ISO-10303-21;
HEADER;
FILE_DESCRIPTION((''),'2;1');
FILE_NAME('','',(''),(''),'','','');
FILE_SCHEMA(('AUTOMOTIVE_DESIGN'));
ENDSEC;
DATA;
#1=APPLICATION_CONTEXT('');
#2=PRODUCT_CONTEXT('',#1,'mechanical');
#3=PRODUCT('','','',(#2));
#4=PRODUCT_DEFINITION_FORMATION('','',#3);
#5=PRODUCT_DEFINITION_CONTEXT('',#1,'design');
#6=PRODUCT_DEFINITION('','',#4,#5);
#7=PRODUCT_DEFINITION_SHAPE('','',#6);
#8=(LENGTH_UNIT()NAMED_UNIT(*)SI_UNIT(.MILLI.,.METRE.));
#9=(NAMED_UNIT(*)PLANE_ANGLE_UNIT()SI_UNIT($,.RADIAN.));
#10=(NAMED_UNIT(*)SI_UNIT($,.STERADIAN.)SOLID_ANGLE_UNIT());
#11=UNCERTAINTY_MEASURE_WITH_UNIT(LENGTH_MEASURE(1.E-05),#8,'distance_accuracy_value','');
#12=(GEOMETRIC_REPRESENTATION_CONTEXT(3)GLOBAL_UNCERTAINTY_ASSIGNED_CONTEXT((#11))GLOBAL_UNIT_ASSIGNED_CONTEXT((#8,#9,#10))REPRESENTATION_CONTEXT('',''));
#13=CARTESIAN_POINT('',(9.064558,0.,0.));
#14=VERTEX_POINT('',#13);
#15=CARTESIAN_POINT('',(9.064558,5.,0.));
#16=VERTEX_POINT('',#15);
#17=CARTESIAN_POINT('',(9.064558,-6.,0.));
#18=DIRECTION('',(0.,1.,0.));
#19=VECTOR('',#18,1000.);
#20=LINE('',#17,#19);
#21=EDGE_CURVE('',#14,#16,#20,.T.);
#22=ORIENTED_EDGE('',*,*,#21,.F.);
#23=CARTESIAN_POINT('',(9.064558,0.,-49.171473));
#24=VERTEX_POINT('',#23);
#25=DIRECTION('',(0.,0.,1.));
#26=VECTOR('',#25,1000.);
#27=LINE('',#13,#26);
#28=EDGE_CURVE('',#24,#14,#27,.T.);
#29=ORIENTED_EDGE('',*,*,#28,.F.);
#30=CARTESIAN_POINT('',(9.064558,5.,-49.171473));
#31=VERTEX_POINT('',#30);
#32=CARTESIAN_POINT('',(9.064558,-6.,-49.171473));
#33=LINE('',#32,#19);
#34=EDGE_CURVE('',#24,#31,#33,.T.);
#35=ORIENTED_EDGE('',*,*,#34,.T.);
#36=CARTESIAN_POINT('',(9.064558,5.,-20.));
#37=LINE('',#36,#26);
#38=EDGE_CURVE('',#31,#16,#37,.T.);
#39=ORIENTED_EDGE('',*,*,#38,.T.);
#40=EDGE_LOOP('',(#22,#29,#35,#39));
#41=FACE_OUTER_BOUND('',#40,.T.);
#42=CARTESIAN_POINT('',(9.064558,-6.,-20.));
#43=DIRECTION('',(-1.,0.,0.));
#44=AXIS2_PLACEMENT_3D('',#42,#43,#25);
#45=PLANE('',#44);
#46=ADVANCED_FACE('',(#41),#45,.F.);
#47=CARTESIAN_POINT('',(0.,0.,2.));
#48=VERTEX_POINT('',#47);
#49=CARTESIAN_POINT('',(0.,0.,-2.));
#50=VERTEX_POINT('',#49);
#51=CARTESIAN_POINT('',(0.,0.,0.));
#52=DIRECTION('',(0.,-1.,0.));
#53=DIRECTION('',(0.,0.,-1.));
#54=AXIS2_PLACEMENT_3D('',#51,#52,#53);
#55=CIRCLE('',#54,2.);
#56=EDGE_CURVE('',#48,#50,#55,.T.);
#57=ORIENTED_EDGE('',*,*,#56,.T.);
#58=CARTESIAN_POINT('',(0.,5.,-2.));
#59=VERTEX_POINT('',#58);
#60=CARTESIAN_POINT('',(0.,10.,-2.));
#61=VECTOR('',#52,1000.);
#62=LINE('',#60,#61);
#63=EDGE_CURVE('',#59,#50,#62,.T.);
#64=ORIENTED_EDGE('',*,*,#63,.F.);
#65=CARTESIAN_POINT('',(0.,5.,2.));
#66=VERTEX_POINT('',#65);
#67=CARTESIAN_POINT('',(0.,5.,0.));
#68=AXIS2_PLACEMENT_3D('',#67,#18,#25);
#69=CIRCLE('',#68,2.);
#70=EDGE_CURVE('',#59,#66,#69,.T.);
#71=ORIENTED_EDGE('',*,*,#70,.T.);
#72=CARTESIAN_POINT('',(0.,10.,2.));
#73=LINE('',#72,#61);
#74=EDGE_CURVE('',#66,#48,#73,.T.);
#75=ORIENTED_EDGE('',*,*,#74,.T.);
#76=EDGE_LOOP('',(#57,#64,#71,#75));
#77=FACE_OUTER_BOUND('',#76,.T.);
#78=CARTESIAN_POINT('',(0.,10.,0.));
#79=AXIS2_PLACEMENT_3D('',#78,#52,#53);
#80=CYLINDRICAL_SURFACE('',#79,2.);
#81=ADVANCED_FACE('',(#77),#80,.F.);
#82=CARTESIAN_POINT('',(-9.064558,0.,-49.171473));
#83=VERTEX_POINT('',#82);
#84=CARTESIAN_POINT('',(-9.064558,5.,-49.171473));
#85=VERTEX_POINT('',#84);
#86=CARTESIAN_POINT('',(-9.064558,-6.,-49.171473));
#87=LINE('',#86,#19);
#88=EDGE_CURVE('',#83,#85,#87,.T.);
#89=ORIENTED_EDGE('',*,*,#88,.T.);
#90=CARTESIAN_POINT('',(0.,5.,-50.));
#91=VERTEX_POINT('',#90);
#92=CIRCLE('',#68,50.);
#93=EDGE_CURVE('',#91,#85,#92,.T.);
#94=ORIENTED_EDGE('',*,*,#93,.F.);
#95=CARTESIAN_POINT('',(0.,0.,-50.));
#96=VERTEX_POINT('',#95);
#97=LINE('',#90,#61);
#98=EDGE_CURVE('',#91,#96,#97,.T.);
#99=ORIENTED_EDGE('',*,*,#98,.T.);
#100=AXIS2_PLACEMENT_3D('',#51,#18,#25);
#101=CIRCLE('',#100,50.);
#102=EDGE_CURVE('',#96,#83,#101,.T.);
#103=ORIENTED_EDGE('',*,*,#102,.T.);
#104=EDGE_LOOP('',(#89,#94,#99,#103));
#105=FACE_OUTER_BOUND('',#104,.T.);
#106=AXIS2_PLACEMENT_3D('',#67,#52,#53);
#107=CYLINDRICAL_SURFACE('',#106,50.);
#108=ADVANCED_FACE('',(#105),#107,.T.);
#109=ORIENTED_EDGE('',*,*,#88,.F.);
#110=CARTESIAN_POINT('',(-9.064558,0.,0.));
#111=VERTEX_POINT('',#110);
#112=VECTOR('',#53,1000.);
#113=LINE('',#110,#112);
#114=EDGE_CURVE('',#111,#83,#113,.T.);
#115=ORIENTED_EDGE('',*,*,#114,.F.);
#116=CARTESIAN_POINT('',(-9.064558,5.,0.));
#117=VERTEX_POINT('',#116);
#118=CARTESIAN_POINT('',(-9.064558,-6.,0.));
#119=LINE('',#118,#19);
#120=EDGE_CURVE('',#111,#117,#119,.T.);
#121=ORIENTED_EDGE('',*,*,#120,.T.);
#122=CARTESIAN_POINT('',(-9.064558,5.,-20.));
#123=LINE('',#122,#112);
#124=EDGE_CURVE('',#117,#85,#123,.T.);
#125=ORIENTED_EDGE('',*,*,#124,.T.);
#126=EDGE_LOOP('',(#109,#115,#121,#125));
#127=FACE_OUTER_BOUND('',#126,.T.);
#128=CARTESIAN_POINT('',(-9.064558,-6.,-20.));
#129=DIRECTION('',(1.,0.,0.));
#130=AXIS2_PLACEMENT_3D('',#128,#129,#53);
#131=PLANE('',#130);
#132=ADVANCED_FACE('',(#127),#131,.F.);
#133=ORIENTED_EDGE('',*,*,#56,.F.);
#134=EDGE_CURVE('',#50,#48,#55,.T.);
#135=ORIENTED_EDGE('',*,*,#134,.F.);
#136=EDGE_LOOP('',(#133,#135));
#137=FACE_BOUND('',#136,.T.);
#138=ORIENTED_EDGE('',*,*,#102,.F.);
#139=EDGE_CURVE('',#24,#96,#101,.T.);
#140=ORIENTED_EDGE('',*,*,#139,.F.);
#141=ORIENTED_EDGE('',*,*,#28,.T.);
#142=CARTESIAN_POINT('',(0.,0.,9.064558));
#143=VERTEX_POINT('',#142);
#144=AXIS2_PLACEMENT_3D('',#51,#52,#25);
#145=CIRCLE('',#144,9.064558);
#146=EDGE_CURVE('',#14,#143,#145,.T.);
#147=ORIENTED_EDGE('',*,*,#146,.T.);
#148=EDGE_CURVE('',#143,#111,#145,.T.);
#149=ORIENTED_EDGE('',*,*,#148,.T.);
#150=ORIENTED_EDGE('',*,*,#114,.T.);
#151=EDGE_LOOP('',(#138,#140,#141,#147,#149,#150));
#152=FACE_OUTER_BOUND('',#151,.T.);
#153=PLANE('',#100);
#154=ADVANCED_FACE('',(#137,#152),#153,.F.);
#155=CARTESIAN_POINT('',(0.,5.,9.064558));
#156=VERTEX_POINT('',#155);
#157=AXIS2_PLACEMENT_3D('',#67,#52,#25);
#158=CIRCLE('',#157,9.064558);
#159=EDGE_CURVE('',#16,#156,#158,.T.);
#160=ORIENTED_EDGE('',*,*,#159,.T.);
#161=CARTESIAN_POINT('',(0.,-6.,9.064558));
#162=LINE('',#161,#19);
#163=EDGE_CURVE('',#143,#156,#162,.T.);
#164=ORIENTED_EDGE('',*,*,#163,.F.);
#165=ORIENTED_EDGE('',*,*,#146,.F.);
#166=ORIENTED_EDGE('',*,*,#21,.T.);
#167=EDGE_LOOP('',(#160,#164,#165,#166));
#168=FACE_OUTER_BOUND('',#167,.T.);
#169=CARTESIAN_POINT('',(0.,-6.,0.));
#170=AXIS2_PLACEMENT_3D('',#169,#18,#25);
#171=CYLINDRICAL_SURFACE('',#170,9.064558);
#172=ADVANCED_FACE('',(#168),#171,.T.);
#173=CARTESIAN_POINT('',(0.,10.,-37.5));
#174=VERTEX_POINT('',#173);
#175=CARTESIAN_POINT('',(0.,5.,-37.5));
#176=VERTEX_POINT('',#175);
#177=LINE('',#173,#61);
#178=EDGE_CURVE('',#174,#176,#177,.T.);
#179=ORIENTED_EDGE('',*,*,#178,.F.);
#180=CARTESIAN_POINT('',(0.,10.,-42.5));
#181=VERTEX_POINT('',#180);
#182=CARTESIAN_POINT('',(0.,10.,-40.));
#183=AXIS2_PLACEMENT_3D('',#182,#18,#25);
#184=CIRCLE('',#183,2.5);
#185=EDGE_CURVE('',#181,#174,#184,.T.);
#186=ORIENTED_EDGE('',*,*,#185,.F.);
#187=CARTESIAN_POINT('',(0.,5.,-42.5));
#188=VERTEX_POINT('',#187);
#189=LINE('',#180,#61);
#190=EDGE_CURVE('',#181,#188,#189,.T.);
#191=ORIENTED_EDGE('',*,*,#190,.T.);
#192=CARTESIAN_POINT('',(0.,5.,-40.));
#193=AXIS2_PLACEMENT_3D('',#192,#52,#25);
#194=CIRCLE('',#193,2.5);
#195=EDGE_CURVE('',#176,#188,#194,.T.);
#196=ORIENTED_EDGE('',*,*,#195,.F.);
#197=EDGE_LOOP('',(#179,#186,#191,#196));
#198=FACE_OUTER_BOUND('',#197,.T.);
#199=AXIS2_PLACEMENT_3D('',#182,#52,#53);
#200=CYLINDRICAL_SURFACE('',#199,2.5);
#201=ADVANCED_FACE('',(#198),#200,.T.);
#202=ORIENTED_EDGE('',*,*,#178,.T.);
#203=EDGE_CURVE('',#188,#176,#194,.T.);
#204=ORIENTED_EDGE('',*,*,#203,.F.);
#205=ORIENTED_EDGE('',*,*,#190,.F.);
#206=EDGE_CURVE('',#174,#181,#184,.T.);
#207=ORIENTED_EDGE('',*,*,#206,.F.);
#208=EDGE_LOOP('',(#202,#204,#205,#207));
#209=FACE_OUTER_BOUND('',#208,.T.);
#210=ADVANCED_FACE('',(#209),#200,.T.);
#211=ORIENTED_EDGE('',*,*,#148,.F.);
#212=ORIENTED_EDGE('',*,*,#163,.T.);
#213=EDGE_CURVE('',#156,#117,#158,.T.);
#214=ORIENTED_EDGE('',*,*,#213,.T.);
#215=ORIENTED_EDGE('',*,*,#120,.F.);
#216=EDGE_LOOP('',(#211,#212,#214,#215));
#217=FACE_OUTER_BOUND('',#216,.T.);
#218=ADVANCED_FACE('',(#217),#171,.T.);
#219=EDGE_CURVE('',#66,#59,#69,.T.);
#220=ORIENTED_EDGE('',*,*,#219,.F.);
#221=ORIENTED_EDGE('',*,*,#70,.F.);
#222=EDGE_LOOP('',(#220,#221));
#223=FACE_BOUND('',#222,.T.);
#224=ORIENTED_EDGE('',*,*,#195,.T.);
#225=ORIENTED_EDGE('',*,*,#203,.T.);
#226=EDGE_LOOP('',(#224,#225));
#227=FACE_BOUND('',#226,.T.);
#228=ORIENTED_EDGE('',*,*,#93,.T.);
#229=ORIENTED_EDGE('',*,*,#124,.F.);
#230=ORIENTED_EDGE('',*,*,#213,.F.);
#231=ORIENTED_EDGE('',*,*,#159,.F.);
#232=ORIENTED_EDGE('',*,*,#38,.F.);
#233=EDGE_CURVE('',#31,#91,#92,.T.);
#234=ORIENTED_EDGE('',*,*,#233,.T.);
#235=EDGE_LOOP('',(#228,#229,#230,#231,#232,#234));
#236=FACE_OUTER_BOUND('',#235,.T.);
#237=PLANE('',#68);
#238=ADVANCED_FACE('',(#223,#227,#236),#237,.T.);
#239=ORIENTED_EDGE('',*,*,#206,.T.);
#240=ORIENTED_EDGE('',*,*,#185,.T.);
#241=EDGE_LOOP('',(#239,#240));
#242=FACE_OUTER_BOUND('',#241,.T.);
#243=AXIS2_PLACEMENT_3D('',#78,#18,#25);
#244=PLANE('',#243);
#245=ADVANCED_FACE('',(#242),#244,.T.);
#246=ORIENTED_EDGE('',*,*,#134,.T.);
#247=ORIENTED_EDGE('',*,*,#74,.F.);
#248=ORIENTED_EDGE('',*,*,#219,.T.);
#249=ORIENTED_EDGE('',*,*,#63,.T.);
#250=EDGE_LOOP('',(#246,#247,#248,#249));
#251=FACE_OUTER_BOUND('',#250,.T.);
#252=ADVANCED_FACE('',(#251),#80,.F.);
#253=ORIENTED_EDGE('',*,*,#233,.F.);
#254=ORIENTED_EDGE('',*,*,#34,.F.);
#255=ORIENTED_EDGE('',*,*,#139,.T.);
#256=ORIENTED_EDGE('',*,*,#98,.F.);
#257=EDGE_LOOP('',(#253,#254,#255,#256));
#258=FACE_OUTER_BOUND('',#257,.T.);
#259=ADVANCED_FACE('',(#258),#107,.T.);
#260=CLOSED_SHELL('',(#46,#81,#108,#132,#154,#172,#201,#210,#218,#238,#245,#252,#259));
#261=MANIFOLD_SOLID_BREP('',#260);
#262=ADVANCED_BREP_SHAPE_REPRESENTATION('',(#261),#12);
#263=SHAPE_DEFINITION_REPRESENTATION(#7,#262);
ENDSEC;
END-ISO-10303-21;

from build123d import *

# Parameters (mm, degrees)
SKETCH_1_3_R        = 50
SKETCH_1_3_R_2      = 2.5
BOSS_EXTRUDE1_DEPTH = 5
SKETCH_1_3_2_R      = 2.5
BOSS_EXTRUDE2_DEPTH = 10
CUT_EXTRUDE1_START  = -11
CUT_EXTRUDE1_DEPTH  = 11
SKETCH2_R           = 2
CUT_EXTRUDE2_DEPTH  = 52.789634215


with BuildPart() as part:
    # Sketch 1_3 → Boss-Extrude1 (new body)
    # profile 1 of 2: a face of its own
    with BuildSketch(Plane(origin=(0, 0, 0), x_dir=(1, 0, 0), z_dir=(0, 1, 0))):
        with Locations(Location((0, 0, 0), (0, 0, 270))):
            Circle(SKETCH_1_3_R)
        with Locations((0, 40)):
            Circle(SKETCH_1_3_R_2, mode=Mode.SUBTRACT)
    # profile 2 of 2: a face of its own
    with BuildSketch(Plane(origin=(0, 0, 0), x_dir=(1, 0, 0), z_dir=(0, 1, 0))):
        with Locations((0, 40)):
            Circle(SKETCH_1_3_R_2)
    extrude(amount=BOSS_EXTRUDE1_DEPTH)

    # Sketch 1_3 2 → Boss-Extrude2 (add)
    with BuildSketch(Plane(origin=(0, 0, 0), x_dir=(1, 0, 0), z_dir=(0, 1, 0))):
        with Locations(Location((0, 40, 0), (0, 0, 270))):
            Circle(SKETCH_1_3_2_R)
    extrude(amount=BOSS_EXTRUDE2_DEPTH)

    # Sketch5 → Cut-Extrude1 (cut)
    with BuildSketch(Plane(origin=(0, 5, 0), x_dir=(1, 0, 0), z_dir=(0, 1, 0)).offset(CUT_EXTRUDE1_START)):
        with BuildLine():
            Line((9.064558023, 20), (9.064558023, 0))
            ThreePointArc((9.064558023, 0), (0, -9.064558023), (-9.064558023, 0))
            Line((-9.064558023, 0), (-9.064558023, 20))
            Line((-9.064558023, 20), (-9.064558023, 49.171473314))
            ThreePointArc((-9.064558023, 49.171473314), (0, -50), (9.064558023, 49.171473314))
            Line((9.064558023, 49.171473314), (9.064558023, 20))
        make_face()
    extrude(amount=CUT_EXTRUDE1_DEPTH, mode=Mode.SUBTRACT)

    # Sketch2 → Cut-Extrude2 (cut, through all)
    with BuildSketch(Plane.XZ):
        with Locations(Location((0, 0, 0), (0, 0, 270))):
            Circle(SKETCH2_R)
    extrude(amount=-CUT_EXTRUDE2_DEPTH, mode=Mode.SUBTRACT)


solid = part.part
